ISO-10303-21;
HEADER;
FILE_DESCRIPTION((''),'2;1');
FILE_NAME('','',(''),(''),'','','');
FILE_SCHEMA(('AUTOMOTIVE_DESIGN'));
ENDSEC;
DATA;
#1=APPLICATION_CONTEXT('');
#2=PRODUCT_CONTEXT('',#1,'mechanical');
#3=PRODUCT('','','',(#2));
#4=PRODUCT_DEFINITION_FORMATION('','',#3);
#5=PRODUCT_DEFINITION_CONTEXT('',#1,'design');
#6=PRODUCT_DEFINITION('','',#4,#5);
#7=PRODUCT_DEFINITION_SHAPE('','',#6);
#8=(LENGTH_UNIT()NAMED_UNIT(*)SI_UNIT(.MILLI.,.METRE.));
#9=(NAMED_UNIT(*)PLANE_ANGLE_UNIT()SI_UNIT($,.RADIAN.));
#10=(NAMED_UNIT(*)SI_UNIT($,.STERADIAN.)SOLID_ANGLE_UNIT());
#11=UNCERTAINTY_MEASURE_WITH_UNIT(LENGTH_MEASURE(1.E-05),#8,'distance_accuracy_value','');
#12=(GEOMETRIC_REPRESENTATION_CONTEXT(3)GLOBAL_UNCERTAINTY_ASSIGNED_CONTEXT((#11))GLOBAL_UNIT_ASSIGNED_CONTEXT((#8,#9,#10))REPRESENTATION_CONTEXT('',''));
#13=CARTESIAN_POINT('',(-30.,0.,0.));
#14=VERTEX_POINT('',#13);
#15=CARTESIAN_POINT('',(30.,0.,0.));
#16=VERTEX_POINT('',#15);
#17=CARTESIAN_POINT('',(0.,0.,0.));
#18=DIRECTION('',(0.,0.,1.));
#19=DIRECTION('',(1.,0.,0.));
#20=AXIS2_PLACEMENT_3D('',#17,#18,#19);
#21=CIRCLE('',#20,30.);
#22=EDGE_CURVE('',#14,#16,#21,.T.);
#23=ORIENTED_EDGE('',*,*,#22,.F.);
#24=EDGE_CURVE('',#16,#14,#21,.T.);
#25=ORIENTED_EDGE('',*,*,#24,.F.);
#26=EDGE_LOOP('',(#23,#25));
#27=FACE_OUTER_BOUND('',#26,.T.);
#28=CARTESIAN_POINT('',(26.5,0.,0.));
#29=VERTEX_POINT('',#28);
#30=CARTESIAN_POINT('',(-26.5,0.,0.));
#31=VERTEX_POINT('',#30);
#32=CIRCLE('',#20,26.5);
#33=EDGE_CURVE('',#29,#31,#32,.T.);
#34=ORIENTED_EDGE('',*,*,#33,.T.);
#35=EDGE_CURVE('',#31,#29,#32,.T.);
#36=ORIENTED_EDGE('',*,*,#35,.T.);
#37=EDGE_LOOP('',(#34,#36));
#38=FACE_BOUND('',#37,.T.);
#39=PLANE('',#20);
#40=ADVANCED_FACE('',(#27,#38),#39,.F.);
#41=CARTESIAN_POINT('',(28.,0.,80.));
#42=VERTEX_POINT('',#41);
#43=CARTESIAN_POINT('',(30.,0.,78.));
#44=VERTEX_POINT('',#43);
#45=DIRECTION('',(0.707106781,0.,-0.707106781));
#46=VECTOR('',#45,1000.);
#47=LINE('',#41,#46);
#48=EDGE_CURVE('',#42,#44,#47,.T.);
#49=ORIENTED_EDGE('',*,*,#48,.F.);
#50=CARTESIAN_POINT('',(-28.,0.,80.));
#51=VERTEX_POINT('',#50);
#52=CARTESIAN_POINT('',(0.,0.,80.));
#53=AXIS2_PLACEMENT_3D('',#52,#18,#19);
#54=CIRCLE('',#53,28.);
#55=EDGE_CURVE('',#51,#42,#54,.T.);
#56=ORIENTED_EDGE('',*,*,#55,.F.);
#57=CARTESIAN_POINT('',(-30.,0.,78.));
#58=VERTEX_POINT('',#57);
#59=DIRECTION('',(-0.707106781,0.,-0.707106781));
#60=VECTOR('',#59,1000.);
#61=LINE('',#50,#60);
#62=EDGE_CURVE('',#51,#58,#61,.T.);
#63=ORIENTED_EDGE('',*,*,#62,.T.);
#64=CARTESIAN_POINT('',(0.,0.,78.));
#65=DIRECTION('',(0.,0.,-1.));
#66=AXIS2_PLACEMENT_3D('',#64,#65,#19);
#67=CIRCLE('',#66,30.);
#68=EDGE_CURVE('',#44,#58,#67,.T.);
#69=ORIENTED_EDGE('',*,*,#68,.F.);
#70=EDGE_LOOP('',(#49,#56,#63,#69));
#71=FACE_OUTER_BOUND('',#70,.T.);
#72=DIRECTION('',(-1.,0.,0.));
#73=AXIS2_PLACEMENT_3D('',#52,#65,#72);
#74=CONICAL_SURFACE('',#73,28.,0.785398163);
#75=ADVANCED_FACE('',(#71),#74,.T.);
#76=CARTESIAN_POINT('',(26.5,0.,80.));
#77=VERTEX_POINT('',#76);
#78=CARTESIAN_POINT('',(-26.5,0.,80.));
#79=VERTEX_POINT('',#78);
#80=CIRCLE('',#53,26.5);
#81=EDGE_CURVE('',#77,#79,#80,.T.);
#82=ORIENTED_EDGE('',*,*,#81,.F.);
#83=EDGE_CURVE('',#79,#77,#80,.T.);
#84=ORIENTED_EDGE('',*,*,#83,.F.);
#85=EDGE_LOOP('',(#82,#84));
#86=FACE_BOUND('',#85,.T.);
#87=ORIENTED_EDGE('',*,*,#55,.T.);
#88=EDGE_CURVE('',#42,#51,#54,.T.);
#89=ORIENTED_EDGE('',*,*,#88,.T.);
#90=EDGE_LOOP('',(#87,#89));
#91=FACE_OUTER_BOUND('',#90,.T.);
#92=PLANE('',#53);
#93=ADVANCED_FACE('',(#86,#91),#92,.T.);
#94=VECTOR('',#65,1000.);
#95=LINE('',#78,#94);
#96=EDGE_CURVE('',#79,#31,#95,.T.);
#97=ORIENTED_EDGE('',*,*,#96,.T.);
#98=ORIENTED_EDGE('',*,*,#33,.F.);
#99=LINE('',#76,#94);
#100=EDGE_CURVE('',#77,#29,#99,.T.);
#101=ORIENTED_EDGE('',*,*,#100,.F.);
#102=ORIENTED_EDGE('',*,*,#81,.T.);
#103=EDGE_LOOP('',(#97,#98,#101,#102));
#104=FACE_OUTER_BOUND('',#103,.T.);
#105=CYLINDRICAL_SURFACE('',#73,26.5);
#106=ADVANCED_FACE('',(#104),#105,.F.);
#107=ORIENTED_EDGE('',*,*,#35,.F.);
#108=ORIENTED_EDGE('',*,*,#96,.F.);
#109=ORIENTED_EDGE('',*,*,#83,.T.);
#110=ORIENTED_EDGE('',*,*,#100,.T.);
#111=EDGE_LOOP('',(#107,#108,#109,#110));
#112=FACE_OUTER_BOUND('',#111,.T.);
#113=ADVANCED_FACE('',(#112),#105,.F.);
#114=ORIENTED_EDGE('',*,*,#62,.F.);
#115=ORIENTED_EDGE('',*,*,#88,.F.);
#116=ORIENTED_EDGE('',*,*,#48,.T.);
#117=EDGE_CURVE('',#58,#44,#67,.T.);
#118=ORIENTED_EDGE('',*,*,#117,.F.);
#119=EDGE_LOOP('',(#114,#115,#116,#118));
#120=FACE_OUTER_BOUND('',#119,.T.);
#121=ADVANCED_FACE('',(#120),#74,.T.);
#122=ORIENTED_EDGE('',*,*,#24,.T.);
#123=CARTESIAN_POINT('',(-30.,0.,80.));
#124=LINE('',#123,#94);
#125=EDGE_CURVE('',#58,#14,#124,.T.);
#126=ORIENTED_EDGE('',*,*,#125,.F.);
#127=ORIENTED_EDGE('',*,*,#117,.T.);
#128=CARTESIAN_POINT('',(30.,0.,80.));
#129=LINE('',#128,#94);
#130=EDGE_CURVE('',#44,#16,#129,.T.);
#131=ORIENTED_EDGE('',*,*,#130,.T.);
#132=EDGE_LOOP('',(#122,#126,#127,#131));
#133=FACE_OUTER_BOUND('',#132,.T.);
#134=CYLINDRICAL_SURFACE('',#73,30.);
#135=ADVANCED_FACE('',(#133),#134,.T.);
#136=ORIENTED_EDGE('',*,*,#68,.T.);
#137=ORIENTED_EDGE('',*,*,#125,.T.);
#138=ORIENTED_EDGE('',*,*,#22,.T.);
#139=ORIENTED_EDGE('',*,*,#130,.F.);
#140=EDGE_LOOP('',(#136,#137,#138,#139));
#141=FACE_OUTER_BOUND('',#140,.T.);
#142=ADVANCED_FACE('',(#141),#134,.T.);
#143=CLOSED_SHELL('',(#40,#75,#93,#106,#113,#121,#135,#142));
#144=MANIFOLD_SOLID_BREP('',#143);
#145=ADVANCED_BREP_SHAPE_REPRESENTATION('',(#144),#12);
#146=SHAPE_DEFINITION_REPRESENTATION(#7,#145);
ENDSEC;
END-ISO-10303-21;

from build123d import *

# Parameters (mm, degrees)
SKETCH_1_R      = 30
SKETCH_1_R_2    = 26.5
EXTRUDE_1_DEPTH = 80
CHAMFER_1_SIZE  = 2


with BuildPart() as part:
    # 草图1 → 拉伸1 (new body)
    with BuildSketch(Plane.XY):
        Circle(SKETCH_1_R)
        Circle(SKETCH_1_R_2, mode=Mode.SUBTRACT)
    extrude(amount=EXTRUDE_1_DEPTH)

    # 倒角1
    chamfer_1_edges = [part.edges().sort_by_distance(p)[0] for p in [
        (-30, 0, 80),
    ]]
    chamfer(chamfer_1_edges, length=CHAMFER_1_SIZE)


solid = part.part
